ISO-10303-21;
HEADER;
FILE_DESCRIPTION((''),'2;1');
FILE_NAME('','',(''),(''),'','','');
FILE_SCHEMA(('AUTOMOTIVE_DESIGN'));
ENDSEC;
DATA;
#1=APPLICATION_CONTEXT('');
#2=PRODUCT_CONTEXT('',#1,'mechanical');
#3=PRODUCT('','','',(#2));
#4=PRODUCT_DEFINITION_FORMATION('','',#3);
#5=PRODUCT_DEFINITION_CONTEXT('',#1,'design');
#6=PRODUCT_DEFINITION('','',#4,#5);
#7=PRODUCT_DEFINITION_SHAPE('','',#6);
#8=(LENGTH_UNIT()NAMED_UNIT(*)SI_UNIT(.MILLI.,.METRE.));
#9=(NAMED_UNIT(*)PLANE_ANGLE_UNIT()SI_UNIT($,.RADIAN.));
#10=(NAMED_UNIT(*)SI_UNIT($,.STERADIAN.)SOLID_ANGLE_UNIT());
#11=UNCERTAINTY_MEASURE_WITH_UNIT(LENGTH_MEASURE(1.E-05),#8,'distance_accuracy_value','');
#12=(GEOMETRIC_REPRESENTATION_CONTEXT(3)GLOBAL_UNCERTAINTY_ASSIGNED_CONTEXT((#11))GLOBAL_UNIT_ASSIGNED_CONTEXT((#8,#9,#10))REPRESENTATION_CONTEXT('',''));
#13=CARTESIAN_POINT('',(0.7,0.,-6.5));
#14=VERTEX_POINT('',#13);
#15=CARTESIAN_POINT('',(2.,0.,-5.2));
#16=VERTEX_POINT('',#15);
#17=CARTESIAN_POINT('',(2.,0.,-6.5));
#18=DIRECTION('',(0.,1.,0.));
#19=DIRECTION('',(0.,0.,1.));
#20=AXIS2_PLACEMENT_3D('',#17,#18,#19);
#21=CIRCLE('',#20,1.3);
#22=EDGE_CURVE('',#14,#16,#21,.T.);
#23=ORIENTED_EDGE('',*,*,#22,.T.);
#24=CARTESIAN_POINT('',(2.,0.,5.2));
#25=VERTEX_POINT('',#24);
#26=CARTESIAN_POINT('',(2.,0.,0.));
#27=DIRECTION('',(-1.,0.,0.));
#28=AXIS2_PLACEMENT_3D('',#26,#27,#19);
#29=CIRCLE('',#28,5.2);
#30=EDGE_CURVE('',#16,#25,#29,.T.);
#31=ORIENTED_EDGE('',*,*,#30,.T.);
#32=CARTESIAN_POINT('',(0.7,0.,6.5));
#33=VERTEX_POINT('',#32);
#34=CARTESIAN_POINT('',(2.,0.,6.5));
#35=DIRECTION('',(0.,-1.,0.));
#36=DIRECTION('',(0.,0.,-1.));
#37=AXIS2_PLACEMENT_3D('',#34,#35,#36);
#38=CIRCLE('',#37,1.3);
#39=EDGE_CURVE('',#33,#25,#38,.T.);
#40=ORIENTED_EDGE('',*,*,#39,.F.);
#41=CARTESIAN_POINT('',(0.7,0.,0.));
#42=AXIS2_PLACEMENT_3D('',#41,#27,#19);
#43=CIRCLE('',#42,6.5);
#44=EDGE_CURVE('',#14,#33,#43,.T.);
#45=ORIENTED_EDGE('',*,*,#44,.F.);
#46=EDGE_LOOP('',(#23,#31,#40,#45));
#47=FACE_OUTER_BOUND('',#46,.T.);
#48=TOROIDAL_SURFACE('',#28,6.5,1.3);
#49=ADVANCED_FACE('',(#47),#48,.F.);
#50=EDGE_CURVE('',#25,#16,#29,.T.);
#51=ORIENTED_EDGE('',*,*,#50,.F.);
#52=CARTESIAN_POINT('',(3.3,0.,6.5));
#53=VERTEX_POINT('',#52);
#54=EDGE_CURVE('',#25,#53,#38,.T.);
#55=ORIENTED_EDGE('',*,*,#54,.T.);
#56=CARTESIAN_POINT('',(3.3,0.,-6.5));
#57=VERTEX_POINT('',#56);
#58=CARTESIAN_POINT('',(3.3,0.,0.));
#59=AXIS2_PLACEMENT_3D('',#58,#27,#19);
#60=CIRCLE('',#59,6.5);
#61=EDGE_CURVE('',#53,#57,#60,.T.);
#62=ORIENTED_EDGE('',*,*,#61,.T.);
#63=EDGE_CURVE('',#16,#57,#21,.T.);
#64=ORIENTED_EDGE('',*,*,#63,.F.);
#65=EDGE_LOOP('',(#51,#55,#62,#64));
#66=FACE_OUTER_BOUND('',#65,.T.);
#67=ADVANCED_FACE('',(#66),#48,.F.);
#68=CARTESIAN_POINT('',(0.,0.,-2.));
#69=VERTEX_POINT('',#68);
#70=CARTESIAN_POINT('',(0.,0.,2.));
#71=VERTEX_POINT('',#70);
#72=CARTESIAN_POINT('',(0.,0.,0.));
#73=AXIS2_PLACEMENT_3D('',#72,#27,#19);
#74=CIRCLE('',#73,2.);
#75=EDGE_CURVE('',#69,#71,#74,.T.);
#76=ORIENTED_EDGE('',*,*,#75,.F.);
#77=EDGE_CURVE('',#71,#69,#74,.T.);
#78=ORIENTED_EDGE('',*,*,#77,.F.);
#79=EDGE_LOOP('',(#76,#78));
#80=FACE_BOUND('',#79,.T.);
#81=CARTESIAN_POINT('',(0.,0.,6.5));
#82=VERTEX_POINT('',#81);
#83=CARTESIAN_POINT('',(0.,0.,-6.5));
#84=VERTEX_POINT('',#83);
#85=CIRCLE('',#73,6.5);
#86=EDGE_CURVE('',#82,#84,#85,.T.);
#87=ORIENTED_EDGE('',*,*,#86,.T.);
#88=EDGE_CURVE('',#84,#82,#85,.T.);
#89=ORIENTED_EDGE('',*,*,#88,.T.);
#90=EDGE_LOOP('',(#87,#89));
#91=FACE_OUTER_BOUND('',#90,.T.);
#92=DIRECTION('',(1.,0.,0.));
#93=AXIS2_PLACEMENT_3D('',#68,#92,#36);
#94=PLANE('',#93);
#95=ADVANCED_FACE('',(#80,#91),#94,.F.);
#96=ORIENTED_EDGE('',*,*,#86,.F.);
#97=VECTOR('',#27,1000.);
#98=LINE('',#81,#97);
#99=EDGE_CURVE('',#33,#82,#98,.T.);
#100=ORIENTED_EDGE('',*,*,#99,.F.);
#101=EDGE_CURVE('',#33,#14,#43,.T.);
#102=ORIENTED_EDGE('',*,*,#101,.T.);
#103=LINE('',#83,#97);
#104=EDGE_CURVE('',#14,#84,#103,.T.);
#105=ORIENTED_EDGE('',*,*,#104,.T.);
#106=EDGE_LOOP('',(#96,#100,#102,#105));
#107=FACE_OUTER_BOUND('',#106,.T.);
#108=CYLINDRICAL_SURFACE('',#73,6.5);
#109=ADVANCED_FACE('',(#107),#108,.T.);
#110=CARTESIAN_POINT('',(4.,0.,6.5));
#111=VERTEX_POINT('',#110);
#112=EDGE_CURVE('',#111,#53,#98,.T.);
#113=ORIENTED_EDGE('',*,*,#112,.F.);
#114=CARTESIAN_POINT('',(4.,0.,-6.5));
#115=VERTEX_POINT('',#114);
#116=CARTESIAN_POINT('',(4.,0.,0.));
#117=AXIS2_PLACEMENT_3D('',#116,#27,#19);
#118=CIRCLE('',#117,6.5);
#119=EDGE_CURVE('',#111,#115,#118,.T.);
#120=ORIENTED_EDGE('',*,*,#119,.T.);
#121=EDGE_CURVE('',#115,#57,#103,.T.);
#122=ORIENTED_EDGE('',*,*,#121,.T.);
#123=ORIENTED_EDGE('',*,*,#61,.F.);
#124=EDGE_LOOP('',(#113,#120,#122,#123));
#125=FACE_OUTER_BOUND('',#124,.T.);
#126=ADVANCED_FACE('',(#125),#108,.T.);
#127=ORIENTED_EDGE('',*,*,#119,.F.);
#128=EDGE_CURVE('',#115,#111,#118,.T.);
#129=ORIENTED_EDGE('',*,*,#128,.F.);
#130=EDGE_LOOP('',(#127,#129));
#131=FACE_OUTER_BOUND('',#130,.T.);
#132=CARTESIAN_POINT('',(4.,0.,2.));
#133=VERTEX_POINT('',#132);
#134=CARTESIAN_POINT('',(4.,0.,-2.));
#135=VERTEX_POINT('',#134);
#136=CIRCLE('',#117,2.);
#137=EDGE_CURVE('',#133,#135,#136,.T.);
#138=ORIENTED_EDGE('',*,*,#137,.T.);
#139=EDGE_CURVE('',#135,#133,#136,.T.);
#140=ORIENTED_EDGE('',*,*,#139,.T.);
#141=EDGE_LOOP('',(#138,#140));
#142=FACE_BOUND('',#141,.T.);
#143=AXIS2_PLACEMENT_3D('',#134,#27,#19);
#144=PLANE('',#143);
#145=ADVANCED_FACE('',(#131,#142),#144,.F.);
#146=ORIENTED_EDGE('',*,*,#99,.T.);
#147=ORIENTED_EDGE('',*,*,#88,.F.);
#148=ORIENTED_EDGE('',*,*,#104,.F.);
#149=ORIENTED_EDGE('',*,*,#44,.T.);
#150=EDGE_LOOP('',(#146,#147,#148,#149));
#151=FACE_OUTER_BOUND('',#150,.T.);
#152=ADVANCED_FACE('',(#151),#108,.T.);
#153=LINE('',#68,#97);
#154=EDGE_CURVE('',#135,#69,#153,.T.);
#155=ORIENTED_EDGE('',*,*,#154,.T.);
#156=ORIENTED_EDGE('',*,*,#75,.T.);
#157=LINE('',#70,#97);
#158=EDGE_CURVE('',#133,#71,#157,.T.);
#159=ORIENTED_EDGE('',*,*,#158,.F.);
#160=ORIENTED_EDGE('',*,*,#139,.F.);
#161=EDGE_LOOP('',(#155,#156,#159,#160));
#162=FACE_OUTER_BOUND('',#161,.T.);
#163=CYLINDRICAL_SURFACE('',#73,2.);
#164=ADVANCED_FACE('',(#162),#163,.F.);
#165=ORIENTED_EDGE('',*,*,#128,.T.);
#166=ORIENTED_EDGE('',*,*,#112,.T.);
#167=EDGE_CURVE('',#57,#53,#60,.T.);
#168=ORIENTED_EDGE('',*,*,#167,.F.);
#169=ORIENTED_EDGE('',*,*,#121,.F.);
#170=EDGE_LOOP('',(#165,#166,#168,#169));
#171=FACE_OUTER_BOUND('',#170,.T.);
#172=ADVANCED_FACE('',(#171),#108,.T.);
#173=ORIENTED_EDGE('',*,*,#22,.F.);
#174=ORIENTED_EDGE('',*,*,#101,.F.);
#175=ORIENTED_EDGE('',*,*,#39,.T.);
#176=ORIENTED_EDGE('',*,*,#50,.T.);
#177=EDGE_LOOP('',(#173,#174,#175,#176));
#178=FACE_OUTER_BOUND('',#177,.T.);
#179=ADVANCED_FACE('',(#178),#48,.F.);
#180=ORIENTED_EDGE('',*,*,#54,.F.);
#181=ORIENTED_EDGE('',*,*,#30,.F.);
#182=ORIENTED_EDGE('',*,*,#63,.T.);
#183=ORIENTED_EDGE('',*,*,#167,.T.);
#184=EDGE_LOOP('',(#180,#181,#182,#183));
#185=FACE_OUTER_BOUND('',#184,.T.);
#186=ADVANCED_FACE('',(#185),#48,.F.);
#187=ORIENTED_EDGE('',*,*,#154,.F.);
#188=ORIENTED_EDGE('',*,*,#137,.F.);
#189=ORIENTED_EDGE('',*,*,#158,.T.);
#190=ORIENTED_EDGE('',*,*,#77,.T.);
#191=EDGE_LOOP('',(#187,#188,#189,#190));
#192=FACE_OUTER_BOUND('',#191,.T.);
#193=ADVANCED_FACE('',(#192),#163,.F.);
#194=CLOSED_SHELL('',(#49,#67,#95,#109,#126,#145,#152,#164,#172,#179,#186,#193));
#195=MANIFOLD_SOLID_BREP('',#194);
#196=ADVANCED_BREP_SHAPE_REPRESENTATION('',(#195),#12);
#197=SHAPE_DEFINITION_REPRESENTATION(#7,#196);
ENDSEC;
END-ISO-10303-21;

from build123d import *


with BuildPart() as part:
    # Sketch1 → Revolve1 (revolve)
    with BuildSketch(Plane(origin=(0, 0, 0), x_dir=(1, 0, 0), z_dir=(0, 1, 0)), mode=Mode.PRIVATE) as revolve1_sk:
        with BuildLine():
            Line((0, 2), (4, 2))
            Line((4, 2), (4, 6.5))
            Line((4, 6.5), (3.3, 6.5))
            ThreePointArc((3.3, 6.5), (2, 5.2), (0.7, 6.5))
            Line((0.7, 6.5), (0, 6.5))
            Line((0, 6.5), (0, 2))
        make_face()
    revolve(revolve1_sk.sketch.rotate(Axis((0, 0, 0), (1, 0, 0)), 180), axis=Axis((0, 0, 0), (1, 0, 0)))


solid = part.part
